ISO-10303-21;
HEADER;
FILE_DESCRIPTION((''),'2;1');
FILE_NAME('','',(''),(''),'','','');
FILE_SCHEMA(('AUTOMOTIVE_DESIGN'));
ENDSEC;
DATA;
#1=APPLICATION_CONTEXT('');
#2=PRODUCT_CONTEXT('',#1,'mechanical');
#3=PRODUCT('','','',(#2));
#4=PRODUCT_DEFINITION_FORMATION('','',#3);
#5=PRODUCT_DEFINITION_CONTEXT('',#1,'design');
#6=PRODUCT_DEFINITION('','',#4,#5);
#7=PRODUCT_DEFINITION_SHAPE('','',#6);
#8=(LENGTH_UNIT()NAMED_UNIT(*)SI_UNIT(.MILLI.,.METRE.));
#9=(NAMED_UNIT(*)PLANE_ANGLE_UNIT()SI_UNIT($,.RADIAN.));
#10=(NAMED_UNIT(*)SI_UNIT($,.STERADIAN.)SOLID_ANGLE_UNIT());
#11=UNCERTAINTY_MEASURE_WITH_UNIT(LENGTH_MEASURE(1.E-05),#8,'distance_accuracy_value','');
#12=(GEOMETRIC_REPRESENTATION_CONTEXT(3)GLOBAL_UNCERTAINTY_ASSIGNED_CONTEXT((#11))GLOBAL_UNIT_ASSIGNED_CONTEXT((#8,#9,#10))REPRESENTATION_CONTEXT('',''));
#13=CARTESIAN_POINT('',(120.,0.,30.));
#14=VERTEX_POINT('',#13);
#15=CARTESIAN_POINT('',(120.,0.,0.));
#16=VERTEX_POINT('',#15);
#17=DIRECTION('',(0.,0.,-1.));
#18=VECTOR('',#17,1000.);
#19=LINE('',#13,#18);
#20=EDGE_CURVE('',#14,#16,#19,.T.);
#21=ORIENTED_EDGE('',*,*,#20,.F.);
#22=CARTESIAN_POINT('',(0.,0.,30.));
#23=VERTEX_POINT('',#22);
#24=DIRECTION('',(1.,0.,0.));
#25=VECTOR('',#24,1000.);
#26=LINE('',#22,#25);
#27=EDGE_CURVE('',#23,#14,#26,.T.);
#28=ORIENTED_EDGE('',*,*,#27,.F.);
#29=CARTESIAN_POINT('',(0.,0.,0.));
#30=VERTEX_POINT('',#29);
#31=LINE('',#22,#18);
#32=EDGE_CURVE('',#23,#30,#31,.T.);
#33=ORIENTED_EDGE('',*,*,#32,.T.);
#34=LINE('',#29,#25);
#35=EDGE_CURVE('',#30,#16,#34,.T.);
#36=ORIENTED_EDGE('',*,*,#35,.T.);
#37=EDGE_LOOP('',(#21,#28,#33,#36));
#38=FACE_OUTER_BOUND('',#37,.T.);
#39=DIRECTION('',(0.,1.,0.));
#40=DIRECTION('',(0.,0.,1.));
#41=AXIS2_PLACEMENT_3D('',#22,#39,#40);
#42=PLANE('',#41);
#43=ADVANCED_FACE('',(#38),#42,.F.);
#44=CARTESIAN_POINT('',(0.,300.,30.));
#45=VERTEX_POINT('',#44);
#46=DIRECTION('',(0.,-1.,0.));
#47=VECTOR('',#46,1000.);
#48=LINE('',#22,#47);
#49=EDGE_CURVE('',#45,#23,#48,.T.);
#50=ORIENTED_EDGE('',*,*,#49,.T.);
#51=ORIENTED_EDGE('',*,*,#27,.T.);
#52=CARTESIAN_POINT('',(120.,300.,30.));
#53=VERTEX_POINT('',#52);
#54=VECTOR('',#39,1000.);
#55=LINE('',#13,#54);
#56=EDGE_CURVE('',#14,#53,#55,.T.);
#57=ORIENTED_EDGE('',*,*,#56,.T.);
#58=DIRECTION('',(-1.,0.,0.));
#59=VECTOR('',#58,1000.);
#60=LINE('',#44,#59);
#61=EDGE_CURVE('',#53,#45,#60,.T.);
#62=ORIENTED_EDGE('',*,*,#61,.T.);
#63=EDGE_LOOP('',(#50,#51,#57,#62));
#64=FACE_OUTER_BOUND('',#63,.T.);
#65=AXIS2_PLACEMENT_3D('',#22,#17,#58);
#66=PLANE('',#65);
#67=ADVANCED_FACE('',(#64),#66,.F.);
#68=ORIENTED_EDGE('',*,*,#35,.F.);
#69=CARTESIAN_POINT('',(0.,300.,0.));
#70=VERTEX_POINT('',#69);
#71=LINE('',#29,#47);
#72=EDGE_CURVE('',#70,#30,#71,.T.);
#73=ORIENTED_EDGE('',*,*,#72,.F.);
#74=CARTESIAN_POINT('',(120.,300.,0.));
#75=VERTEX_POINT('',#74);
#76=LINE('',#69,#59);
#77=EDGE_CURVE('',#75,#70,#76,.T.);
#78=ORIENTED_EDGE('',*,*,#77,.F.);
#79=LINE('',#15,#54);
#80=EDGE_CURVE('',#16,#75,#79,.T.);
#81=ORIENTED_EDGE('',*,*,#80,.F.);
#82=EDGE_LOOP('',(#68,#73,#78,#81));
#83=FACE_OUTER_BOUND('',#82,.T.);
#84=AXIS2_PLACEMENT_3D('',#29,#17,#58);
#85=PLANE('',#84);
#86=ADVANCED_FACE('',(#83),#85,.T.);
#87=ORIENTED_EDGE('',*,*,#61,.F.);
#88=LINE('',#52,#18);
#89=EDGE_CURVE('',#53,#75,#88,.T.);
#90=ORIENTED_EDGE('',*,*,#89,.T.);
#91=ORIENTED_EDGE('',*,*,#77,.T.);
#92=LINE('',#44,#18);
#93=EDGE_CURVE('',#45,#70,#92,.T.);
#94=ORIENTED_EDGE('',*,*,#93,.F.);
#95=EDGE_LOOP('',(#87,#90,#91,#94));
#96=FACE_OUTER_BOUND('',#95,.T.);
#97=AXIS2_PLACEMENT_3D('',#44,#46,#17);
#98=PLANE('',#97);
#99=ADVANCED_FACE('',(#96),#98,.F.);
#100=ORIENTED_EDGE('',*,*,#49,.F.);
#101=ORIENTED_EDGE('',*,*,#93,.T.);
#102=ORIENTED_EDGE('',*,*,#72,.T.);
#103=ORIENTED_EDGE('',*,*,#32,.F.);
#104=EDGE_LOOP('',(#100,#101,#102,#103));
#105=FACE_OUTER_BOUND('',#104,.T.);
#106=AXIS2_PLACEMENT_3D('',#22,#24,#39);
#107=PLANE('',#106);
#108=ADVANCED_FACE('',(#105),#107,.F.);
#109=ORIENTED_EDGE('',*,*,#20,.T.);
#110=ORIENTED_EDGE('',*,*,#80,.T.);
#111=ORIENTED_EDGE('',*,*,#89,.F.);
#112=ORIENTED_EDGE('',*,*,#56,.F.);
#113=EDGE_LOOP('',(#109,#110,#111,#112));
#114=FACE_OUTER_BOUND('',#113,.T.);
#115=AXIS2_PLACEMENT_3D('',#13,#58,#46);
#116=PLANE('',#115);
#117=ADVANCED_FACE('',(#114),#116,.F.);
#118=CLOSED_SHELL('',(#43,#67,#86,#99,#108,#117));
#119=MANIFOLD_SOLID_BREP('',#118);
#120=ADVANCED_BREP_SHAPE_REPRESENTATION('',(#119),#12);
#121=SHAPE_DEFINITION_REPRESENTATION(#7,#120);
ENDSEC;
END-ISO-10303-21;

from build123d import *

# Parameters (mm, degrees)
SKETCH1_W           = 120
SKETCH1_H           = 300
BOSS_EXTRUDE1_DEPTH = 30


with BuildPart() as part:
    # Sketch1 → Boss-Extrude1 (new body)
    with BuildSketch(Plane.XY):
        with Locations((60, 150)):
            Rectangle(SKETCH1_W, SKETCH1_H)
    extrude(amount=BOSS_EXTRUDE1_DEPTH)


solid = part.part
